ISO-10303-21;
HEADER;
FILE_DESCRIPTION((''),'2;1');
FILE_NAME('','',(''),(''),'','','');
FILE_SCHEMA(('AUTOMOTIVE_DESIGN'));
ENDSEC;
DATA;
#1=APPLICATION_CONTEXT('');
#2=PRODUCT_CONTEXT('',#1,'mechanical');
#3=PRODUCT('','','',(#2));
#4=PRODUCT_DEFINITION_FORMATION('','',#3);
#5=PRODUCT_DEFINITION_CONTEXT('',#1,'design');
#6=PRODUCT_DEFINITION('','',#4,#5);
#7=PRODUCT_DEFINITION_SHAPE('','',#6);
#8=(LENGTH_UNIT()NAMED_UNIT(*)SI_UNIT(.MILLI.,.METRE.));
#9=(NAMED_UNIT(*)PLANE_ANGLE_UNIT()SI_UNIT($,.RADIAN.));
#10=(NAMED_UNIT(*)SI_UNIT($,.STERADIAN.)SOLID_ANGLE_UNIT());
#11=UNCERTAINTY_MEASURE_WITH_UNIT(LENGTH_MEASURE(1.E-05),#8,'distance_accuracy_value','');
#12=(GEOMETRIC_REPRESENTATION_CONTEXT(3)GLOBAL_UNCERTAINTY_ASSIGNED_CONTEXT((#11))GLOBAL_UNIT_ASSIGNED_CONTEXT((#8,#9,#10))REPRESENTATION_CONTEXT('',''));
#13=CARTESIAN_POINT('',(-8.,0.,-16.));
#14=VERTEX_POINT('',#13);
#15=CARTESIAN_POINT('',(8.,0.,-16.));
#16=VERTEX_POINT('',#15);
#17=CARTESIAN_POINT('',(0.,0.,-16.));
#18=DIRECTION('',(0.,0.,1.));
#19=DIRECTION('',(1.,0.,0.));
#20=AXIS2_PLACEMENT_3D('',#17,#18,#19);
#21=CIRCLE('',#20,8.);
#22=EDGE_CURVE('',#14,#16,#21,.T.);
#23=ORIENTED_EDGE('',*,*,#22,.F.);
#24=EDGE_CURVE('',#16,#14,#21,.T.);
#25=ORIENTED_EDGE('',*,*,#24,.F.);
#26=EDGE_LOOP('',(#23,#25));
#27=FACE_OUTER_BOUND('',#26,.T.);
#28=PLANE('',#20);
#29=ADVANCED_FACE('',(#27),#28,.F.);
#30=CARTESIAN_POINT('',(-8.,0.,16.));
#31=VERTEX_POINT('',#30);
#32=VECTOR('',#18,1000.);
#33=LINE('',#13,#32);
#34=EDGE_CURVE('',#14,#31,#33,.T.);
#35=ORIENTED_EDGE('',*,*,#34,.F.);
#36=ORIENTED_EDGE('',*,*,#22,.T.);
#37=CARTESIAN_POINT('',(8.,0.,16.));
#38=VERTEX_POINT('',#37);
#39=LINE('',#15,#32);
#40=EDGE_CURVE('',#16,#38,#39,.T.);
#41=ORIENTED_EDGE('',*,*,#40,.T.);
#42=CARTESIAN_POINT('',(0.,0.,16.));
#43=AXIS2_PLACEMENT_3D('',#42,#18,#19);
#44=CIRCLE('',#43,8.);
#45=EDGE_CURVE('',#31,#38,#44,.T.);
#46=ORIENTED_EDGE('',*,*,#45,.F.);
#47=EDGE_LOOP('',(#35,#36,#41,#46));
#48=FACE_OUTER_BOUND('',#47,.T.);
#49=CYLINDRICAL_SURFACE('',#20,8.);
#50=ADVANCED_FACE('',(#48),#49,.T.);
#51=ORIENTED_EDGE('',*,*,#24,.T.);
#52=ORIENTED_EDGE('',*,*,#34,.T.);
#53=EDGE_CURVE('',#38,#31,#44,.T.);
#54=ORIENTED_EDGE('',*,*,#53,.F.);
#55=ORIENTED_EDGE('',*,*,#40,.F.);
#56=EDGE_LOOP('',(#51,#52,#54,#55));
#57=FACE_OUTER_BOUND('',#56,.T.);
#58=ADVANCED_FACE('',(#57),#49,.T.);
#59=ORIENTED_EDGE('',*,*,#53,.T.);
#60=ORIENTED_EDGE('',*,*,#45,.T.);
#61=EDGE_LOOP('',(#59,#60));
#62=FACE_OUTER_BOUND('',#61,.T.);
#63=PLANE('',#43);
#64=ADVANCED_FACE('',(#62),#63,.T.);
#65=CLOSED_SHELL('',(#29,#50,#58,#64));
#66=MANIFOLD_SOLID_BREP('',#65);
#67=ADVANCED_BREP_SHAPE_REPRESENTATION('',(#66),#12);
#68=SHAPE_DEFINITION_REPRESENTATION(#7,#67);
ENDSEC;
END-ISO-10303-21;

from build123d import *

# Parameters (mm, degrees)
SKETCH_1_R      = 8
EXTRUDE_1_DEPTH = 16


with BuildPart() as part:
    # 草图1 → 凸台-拉伸1 (new, symmetric)
    with BuildSketch(Plane.XY):
        Circle(SKETCH_1_R)
    extrude(amount=EXTRUDE_1_DEPTH, both=True)


solid = part.part
